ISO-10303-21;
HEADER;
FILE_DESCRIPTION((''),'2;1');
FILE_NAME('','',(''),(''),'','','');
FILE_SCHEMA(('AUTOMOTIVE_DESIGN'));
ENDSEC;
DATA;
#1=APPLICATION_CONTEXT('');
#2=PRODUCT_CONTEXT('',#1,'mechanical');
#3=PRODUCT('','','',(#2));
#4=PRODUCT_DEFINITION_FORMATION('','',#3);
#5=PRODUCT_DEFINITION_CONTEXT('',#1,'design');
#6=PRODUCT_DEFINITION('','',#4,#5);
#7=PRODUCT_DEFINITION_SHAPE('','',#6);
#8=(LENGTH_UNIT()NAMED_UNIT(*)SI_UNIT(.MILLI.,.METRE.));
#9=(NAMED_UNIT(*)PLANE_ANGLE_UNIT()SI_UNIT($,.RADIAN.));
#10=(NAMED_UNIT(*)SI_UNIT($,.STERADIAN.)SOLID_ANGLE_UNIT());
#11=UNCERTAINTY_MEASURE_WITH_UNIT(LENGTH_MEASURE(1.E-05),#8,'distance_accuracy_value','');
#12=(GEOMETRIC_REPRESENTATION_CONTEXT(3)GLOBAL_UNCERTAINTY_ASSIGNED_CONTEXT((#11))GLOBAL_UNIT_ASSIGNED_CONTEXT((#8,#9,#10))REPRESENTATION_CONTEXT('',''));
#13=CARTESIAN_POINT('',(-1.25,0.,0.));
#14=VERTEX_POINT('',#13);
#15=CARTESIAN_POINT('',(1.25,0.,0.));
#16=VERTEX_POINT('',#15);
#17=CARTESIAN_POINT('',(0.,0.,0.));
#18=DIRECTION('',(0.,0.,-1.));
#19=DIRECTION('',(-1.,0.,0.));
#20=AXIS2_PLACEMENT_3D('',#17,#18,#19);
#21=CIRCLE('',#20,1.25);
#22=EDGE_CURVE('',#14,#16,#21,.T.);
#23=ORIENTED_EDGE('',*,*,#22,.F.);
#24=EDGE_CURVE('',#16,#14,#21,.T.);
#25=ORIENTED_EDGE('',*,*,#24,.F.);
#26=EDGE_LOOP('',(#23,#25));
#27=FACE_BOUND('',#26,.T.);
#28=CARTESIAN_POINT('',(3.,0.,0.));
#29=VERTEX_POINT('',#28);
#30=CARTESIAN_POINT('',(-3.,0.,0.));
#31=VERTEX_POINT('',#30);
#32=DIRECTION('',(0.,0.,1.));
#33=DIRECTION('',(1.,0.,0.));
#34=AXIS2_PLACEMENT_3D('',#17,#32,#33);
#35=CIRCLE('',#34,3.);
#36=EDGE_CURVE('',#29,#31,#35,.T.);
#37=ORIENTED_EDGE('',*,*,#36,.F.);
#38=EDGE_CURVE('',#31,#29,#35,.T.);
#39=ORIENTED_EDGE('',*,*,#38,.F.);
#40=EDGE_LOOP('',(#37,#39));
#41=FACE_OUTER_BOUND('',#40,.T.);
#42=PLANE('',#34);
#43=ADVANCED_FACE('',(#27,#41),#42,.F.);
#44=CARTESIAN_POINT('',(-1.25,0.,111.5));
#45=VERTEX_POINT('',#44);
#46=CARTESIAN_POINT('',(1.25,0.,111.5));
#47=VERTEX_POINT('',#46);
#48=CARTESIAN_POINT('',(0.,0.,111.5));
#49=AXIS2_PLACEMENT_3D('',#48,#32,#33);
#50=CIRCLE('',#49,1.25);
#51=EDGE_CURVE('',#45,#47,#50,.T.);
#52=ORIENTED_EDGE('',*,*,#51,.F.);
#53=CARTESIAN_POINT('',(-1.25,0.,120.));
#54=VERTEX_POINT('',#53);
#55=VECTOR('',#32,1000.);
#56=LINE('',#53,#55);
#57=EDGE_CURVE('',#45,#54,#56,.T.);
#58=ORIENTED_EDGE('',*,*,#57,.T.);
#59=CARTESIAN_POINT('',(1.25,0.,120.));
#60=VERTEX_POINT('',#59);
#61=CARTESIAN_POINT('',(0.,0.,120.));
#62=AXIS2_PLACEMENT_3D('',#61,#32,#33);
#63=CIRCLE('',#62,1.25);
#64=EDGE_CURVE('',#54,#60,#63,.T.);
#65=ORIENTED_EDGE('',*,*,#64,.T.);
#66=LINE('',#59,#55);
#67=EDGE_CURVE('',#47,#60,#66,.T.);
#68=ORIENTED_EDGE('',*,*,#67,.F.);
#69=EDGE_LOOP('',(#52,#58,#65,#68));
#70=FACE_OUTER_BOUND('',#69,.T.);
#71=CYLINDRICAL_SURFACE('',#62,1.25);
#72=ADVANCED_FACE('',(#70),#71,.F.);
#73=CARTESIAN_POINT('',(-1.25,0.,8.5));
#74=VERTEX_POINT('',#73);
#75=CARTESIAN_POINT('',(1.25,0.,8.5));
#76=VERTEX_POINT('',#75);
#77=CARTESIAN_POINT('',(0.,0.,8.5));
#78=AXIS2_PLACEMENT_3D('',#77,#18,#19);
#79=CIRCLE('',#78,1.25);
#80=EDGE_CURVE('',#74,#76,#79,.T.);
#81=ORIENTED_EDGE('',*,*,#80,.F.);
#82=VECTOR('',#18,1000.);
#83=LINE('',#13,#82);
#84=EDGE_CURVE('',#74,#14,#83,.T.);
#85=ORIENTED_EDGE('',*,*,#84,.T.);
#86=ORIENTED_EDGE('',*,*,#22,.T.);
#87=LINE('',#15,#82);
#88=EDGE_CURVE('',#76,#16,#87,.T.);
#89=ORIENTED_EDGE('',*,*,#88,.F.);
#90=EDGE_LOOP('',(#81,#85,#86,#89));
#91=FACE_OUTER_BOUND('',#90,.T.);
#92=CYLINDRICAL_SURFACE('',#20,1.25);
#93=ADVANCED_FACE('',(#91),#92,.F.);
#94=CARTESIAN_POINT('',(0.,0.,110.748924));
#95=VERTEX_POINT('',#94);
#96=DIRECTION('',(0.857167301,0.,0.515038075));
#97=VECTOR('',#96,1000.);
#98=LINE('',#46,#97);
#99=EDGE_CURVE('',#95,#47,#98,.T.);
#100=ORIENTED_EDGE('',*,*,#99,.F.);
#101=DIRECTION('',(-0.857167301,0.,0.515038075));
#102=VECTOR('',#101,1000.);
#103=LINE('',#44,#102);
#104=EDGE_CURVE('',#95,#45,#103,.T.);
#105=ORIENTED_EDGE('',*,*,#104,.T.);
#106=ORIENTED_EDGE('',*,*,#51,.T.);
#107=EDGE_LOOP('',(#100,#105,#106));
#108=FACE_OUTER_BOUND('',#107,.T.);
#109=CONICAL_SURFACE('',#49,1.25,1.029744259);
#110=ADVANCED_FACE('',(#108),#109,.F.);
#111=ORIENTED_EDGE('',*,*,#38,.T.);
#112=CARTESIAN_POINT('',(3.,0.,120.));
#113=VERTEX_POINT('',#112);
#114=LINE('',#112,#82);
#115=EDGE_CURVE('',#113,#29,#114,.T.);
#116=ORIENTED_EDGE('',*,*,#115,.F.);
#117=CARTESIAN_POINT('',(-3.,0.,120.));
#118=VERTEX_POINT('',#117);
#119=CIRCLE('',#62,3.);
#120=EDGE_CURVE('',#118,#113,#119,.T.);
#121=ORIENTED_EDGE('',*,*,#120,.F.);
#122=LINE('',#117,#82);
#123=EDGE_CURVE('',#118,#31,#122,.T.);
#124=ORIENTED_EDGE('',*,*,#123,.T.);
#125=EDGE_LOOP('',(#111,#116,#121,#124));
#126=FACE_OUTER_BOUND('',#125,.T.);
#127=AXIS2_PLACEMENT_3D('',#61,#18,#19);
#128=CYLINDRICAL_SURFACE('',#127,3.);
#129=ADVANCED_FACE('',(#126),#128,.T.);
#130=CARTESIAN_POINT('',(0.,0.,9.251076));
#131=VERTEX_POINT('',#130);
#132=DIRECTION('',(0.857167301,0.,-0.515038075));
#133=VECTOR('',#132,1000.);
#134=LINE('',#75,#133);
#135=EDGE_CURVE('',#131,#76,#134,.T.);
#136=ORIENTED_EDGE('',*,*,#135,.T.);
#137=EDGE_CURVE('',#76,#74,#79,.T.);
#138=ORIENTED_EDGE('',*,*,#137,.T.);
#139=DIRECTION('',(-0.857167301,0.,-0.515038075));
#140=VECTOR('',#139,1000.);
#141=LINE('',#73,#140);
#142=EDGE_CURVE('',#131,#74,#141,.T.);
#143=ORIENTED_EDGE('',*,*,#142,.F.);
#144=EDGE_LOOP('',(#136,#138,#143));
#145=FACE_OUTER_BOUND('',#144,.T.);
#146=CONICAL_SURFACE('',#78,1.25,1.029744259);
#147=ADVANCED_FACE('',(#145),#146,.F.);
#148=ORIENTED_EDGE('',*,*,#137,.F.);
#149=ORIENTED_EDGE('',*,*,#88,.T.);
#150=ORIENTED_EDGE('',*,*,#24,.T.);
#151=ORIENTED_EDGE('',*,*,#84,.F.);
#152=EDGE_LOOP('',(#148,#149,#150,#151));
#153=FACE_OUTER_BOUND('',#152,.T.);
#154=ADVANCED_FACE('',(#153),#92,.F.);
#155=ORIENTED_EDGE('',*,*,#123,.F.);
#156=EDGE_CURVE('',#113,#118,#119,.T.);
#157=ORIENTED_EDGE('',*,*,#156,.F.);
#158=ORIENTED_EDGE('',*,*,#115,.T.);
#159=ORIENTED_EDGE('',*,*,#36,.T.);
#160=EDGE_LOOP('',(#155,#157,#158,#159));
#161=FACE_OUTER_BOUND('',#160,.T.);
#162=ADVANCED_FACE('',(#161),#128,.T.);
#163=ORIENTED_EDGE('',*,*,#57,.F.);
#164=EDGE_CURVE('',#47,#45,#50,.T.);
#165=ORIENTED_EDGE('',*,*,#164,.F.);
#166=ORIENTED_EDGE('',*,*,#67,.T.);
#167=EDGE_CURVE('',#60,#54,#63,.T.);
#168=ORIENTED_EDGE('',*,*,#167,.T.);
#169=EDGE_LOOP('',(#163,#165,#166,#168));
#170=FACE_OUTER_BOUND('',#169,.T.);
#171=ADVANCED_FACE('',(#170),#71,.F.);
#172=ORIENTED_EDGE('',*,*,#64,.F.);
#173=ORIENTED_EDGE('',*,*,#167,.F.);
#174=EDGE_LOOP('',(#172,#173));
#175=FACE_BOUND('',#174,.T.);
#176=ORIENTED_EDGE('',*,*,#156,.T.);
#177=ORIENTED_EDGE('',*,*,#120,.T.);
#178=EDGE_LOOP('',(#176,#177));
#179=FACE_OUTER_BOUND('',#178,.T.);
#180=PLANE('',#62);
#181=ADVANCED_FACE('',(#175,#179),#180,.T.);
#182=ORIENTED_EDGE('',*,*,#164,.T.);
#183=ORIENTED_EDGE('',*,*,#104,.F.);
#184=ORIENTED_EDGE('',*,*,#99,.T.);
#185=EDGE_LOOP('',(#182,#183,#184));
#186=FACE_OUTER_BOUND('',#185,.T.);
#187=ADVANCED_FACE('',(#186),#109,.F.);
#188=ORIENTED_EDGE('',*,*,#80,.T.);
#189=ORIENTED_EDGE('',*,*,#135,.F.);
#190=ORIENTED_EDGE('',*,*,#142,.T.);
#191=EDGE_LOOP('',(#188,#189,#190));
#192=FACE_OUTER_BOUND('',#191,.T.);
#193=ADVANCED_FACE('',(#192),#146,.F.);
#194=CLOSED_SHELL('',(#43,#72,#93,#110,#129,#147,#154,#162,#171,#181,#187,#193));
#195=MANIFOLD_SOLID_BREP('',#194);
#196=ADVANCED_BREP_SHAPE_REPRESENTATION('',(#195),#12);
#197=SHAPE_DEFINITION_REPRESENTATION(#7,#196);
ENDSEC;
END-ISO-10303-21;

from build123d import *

# Parameters (mm, degrees)
SKETCH1_R             = 3
BOSS_EXTRUDE1_DEPTH   = 120
M3_TAPPED_HOLE1_D     = 2.5
M3_TAPPED_HOLE1_DEPTH = 8.5
M3_TAPPED_HOLE1_TIP   = 0.751075774
M3_TAPPED_HOLE2_D     = 2.5
M3_TAPPED_HOLE2_DEPTH = 8.5
M3_TAPPED_HOLE2_TIP   = 0.751075774


with BuildPart() as part:
    # Sketch1 → Boss-Extrude1 (new body)
    with BuildSketch(Plane.XY):
        Circle(SKETCH1_R)
    extrude(amount=BOSS_EXTRUDE1_DEPTH)

    # M3 Tapped Hole1
    with Locations(Plane.XY.offset(120)):
        with Locations((0, 0)):
            Hole(M3_TAPPED_HOLE1_D / 2, depth=M3_TAPPED_HOLE1_DEPTH)
            with Locations((0, 0, -(M3_TAPPED_HOLE1_DEPTH + M3_TAPPED_HOLE1_TIP / 2))):  # 118° drill point
                Cone(0, M3_TAPPED_HOLE1_D / 2, M3_TAPPED_HOLE1_TIP, mode=Mode.SUBTRACT)

    # M3 Tapped Hole2
    with Locations(Plane(origin=(0, 0, 0), x_dir=(-1, 0, 0), z_dir=(0, 0, -1))):
        with Locations((0, 0)):
            Hole(M3_TAPPED_HOLE2_D / 2, depth=M3_TAPPED_HOLE2_DEPTH)
            with Locations((0, 0, -(M3_TAPPED_HOLE2_DEPTH + M3_TAPPED_HOLE2_TIP / 2))):  # 118° drill point
                Cone(0, M3_TAPPED_HOLE2_D / 2, M3_TAPPED_HOLE2_TIP, mode=Mode.SUBTRACT)


solid = part.part
